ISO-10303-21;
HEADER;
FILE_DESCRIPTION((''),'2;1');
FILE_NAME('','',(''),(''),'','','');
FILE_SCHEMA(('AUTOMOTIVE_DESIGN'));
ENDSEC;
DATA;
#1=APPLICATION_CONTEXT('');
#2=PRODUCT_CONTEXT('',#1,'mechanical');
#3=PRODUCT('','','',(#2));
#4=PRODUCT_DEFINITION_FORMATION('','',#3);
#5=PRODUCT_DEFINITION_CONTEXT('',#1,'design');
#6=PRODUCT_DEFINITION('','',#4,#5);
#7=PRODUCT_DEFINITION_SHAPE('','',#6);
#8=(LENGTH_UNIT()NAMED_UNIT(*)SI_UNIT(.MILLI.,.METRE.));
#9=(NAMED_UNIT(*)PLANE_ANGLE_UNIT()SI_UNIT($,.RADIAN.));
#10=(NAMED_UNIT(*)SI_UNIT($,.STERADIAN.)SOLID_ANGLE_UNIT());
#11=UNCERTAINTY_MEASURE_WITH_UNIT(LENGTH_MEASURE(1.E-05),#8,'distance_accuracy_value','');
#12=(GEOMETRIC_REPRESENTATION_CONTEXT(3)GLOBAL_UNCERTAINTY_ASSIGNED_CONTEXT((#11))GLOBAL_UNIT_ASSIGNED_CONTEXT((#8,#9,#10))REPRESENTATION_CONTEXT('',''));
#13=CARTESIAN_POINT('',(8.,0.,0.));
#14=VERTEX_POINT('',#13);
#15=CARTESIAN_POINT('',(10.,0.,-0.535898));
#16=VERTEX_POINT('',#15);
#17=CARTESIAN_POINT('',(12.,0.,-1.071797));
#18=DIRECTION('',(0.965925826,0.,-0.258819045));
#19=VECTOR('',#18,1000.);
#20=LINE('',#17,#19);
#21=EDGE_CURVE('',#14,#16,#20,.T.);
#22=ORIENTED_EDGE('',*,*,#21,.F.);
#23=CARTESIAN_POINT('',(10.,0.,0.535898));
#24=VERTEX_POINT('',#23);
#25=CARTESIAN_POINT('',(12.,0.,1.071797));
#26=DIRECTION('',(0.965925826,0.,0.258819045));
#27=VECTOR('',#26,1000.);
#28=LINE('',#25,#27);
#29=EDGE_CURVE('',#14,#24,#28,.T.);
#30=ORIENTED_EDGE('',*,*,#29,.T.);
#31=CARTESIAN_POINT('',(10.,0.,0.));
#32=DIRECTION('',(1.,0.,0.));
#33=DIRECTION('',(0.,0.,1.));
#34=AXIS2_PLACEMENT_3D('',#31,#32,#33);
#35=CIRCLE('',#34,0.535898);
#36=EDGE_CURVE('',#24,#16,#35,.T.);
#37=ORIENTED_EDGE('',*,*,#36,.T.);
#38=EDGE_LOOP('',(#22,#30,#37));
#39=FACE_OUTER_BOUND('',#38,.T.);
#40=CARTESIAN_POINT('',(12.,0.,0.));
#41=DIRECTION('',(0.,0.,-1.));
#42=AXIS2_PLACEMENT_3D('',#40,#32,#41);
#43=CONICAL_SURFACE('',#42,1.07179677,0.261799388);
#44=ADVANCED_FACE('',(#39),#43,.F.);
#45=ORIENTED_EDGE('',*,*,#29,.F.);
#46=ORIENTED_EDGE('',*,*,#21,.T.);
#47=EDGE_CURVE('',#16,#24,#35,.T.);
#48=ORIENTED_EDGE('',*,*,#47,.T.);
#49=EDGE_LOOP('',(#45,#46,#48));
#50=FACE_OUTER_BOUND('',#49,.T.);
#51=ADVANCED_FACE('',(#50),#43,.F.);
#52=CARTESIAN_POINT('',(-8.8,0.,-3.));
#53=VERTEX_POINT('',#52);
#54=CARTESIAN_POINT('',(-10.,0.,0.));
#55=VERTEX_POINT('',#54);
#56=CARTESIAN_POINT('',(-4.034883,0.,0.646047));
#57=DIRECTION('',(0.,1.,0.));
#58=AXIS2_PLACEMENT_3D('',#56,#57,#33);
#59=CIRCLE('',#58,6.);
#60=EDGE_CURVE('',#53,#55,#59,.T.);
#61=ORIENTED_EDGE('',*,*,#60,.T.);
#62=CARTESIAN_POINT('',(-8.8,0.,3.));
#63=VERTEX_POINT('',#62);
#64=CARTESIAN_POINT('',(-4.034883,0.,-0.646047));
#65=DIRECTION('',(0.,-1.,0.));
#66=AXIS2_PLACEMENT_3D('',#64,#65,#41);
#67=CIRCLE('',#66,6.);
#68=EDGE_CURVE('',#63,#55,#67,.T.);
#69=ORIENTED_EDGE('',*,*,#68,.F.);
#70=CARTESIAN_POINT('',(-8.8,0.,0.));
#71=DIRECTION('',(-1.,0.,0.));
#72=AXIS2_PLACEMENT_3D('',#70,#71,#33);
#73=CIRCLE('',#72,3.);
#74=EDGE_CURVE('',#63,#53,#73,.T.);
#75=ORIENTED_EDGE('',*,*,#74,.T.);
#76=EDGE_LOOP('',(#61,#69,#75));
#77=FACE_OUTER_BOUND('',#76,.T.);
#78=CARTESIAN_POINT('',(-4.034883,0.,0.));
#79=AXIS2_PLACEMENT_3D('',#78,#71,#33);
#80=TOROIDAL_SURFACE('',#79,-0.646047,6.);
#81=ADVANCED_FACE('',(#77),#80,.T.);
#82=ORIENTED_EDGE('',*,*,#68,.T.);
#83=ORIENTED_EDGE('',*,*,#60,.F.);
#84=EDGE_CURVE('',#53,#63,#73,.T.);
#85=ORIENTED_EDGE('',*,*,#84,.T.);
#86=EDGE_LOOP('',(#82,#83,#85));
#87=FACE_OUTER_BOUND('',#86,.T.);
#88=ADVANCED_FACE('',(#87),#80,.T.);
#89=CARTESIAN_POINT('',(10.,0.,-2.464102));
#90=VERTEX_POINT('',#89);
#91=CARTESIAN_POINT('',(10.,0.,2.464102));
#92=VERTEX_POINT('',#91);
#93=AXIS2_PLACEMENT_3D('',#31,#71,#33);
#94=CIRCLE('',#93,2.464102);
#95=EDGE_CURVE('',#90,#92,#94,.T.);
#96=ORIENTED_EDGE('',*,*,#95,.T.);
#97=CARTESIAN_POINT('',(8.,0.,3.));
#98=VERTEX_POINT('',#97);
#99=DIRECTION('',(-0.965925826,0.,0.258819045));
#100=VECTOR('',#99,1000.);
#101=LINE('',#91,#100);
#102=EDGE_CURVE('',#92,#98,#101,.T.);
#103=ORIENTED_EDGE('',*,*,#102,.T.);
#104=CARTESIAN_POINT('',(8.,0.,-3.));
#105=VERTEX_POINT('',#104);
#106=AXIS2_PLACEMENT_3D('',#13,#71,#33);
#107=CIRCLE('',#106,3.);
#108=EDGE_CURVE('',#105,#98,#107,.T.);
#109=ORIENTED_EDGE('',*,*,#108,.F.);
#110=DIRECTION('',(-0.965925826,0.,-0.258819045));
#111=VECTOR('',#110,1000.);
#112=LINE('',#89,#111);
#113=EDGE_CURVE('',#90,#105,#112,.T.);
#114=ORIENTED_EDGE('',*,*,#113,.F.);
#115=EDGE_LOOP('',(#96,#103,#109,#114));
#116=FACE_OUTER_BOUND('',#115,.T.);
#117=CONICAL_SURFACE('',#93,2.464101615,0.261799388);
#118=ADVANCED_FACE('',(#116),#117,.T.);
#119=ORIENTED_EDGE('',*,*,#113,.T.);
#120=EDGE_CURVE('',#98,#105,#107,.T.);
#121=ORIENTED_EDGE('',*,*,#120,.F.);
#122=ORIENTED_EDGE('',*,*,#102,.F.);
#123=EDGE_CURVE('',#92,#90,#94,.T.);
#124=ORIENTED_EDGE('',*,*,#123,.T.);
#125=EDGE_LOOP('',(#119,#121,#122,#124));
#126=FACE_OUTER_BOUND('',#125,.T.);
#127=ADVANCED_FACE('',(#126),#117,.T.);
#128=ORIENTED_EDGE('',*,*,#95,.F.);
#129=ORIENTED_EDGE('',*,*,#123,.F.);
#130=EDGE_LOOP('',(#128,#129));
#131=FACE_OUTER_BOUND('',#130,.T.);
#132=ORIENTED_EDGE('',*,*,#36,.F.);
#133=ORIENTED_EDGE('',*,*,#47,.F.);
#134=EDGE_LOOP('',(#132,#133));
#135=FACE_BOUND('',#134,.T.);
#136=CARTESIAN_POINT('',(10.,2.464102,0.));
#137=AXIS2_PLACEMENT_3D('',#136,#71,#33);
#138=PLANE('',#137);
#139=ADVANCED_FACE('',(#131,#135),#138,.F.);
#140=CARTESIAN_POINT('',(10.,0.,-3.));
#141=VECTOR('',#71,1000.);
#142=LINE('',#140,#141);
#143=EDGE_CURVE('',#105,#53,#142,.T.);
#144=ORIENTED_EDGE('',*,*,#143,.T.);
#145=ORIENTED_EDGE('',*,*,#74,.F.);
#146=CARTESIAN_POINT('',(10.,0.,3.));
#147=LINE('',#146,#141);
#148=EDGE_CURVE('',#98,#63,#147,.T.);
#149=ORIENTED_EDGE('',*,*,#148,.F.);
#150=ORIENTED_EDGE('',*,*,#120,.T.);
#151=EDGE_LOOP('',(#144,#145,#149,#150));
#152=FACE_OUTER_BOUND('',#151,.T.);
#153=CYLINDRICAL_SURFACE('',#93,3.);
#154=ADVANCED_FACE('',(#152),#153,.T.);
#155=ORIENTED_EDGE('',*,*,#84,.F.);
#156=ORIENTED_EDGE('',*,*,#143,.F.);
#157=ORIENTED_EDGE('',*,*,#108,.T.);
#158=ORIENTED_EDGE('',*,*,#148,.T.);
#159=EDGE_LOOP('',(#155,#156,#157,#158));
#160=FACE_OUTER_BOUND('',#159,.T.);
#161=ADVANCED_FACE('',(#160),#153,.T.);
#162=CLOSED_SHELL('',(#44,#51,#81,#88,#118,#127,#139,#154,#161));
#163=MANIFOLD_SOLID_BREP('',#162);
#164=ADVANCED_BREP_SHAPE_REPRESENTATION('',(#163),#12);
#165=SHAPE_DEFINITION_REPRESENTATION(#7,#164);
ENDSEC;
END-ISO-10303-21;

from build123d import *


with BuildPart() as part:
    # 草图1 → 旋转1 (revolve)
    with BuildSketch(Plane.XY, mode=Mode.PRIVATE) as revolve_1_sk:
        with BuildLine():
            Line((-8.8, 3), (8, 3))
            Line((8, 3), (10, 2.464101615))
            Line((10, 2.464101615), (10, 0))
            Line((10, 0), (-10, 0))
            ThreePointArc((-10, 0), (-9.605742928, 1.582297171), (-8.8, 3))
        make_face()
    revolve(revolve_1_sk.sketch.rotate(Axis((10, 0, 0), (-1, 0, 0)), 270), axis=Axis((10, 0, 0), (-1, 0, 0)))

    # 草图2 → 切除-旋转1 (revolve, cut)
    with BuildSketch(Plane.XY, mode=Mode.PRIVATE) as cut_revolve_1_sk:
        Polygon((8, 0), (12, 1.07179677), (12, 0), align=None)
    revolve(cut_revolve_1_sk.sketch.rotate(Axis((12, 0, 0), (-1, 0, 0)), 90), axis=Axis((12, 0, 0), (-1, 0, 0)), mode=Mode.SUBTRACT)


solid = part.part
